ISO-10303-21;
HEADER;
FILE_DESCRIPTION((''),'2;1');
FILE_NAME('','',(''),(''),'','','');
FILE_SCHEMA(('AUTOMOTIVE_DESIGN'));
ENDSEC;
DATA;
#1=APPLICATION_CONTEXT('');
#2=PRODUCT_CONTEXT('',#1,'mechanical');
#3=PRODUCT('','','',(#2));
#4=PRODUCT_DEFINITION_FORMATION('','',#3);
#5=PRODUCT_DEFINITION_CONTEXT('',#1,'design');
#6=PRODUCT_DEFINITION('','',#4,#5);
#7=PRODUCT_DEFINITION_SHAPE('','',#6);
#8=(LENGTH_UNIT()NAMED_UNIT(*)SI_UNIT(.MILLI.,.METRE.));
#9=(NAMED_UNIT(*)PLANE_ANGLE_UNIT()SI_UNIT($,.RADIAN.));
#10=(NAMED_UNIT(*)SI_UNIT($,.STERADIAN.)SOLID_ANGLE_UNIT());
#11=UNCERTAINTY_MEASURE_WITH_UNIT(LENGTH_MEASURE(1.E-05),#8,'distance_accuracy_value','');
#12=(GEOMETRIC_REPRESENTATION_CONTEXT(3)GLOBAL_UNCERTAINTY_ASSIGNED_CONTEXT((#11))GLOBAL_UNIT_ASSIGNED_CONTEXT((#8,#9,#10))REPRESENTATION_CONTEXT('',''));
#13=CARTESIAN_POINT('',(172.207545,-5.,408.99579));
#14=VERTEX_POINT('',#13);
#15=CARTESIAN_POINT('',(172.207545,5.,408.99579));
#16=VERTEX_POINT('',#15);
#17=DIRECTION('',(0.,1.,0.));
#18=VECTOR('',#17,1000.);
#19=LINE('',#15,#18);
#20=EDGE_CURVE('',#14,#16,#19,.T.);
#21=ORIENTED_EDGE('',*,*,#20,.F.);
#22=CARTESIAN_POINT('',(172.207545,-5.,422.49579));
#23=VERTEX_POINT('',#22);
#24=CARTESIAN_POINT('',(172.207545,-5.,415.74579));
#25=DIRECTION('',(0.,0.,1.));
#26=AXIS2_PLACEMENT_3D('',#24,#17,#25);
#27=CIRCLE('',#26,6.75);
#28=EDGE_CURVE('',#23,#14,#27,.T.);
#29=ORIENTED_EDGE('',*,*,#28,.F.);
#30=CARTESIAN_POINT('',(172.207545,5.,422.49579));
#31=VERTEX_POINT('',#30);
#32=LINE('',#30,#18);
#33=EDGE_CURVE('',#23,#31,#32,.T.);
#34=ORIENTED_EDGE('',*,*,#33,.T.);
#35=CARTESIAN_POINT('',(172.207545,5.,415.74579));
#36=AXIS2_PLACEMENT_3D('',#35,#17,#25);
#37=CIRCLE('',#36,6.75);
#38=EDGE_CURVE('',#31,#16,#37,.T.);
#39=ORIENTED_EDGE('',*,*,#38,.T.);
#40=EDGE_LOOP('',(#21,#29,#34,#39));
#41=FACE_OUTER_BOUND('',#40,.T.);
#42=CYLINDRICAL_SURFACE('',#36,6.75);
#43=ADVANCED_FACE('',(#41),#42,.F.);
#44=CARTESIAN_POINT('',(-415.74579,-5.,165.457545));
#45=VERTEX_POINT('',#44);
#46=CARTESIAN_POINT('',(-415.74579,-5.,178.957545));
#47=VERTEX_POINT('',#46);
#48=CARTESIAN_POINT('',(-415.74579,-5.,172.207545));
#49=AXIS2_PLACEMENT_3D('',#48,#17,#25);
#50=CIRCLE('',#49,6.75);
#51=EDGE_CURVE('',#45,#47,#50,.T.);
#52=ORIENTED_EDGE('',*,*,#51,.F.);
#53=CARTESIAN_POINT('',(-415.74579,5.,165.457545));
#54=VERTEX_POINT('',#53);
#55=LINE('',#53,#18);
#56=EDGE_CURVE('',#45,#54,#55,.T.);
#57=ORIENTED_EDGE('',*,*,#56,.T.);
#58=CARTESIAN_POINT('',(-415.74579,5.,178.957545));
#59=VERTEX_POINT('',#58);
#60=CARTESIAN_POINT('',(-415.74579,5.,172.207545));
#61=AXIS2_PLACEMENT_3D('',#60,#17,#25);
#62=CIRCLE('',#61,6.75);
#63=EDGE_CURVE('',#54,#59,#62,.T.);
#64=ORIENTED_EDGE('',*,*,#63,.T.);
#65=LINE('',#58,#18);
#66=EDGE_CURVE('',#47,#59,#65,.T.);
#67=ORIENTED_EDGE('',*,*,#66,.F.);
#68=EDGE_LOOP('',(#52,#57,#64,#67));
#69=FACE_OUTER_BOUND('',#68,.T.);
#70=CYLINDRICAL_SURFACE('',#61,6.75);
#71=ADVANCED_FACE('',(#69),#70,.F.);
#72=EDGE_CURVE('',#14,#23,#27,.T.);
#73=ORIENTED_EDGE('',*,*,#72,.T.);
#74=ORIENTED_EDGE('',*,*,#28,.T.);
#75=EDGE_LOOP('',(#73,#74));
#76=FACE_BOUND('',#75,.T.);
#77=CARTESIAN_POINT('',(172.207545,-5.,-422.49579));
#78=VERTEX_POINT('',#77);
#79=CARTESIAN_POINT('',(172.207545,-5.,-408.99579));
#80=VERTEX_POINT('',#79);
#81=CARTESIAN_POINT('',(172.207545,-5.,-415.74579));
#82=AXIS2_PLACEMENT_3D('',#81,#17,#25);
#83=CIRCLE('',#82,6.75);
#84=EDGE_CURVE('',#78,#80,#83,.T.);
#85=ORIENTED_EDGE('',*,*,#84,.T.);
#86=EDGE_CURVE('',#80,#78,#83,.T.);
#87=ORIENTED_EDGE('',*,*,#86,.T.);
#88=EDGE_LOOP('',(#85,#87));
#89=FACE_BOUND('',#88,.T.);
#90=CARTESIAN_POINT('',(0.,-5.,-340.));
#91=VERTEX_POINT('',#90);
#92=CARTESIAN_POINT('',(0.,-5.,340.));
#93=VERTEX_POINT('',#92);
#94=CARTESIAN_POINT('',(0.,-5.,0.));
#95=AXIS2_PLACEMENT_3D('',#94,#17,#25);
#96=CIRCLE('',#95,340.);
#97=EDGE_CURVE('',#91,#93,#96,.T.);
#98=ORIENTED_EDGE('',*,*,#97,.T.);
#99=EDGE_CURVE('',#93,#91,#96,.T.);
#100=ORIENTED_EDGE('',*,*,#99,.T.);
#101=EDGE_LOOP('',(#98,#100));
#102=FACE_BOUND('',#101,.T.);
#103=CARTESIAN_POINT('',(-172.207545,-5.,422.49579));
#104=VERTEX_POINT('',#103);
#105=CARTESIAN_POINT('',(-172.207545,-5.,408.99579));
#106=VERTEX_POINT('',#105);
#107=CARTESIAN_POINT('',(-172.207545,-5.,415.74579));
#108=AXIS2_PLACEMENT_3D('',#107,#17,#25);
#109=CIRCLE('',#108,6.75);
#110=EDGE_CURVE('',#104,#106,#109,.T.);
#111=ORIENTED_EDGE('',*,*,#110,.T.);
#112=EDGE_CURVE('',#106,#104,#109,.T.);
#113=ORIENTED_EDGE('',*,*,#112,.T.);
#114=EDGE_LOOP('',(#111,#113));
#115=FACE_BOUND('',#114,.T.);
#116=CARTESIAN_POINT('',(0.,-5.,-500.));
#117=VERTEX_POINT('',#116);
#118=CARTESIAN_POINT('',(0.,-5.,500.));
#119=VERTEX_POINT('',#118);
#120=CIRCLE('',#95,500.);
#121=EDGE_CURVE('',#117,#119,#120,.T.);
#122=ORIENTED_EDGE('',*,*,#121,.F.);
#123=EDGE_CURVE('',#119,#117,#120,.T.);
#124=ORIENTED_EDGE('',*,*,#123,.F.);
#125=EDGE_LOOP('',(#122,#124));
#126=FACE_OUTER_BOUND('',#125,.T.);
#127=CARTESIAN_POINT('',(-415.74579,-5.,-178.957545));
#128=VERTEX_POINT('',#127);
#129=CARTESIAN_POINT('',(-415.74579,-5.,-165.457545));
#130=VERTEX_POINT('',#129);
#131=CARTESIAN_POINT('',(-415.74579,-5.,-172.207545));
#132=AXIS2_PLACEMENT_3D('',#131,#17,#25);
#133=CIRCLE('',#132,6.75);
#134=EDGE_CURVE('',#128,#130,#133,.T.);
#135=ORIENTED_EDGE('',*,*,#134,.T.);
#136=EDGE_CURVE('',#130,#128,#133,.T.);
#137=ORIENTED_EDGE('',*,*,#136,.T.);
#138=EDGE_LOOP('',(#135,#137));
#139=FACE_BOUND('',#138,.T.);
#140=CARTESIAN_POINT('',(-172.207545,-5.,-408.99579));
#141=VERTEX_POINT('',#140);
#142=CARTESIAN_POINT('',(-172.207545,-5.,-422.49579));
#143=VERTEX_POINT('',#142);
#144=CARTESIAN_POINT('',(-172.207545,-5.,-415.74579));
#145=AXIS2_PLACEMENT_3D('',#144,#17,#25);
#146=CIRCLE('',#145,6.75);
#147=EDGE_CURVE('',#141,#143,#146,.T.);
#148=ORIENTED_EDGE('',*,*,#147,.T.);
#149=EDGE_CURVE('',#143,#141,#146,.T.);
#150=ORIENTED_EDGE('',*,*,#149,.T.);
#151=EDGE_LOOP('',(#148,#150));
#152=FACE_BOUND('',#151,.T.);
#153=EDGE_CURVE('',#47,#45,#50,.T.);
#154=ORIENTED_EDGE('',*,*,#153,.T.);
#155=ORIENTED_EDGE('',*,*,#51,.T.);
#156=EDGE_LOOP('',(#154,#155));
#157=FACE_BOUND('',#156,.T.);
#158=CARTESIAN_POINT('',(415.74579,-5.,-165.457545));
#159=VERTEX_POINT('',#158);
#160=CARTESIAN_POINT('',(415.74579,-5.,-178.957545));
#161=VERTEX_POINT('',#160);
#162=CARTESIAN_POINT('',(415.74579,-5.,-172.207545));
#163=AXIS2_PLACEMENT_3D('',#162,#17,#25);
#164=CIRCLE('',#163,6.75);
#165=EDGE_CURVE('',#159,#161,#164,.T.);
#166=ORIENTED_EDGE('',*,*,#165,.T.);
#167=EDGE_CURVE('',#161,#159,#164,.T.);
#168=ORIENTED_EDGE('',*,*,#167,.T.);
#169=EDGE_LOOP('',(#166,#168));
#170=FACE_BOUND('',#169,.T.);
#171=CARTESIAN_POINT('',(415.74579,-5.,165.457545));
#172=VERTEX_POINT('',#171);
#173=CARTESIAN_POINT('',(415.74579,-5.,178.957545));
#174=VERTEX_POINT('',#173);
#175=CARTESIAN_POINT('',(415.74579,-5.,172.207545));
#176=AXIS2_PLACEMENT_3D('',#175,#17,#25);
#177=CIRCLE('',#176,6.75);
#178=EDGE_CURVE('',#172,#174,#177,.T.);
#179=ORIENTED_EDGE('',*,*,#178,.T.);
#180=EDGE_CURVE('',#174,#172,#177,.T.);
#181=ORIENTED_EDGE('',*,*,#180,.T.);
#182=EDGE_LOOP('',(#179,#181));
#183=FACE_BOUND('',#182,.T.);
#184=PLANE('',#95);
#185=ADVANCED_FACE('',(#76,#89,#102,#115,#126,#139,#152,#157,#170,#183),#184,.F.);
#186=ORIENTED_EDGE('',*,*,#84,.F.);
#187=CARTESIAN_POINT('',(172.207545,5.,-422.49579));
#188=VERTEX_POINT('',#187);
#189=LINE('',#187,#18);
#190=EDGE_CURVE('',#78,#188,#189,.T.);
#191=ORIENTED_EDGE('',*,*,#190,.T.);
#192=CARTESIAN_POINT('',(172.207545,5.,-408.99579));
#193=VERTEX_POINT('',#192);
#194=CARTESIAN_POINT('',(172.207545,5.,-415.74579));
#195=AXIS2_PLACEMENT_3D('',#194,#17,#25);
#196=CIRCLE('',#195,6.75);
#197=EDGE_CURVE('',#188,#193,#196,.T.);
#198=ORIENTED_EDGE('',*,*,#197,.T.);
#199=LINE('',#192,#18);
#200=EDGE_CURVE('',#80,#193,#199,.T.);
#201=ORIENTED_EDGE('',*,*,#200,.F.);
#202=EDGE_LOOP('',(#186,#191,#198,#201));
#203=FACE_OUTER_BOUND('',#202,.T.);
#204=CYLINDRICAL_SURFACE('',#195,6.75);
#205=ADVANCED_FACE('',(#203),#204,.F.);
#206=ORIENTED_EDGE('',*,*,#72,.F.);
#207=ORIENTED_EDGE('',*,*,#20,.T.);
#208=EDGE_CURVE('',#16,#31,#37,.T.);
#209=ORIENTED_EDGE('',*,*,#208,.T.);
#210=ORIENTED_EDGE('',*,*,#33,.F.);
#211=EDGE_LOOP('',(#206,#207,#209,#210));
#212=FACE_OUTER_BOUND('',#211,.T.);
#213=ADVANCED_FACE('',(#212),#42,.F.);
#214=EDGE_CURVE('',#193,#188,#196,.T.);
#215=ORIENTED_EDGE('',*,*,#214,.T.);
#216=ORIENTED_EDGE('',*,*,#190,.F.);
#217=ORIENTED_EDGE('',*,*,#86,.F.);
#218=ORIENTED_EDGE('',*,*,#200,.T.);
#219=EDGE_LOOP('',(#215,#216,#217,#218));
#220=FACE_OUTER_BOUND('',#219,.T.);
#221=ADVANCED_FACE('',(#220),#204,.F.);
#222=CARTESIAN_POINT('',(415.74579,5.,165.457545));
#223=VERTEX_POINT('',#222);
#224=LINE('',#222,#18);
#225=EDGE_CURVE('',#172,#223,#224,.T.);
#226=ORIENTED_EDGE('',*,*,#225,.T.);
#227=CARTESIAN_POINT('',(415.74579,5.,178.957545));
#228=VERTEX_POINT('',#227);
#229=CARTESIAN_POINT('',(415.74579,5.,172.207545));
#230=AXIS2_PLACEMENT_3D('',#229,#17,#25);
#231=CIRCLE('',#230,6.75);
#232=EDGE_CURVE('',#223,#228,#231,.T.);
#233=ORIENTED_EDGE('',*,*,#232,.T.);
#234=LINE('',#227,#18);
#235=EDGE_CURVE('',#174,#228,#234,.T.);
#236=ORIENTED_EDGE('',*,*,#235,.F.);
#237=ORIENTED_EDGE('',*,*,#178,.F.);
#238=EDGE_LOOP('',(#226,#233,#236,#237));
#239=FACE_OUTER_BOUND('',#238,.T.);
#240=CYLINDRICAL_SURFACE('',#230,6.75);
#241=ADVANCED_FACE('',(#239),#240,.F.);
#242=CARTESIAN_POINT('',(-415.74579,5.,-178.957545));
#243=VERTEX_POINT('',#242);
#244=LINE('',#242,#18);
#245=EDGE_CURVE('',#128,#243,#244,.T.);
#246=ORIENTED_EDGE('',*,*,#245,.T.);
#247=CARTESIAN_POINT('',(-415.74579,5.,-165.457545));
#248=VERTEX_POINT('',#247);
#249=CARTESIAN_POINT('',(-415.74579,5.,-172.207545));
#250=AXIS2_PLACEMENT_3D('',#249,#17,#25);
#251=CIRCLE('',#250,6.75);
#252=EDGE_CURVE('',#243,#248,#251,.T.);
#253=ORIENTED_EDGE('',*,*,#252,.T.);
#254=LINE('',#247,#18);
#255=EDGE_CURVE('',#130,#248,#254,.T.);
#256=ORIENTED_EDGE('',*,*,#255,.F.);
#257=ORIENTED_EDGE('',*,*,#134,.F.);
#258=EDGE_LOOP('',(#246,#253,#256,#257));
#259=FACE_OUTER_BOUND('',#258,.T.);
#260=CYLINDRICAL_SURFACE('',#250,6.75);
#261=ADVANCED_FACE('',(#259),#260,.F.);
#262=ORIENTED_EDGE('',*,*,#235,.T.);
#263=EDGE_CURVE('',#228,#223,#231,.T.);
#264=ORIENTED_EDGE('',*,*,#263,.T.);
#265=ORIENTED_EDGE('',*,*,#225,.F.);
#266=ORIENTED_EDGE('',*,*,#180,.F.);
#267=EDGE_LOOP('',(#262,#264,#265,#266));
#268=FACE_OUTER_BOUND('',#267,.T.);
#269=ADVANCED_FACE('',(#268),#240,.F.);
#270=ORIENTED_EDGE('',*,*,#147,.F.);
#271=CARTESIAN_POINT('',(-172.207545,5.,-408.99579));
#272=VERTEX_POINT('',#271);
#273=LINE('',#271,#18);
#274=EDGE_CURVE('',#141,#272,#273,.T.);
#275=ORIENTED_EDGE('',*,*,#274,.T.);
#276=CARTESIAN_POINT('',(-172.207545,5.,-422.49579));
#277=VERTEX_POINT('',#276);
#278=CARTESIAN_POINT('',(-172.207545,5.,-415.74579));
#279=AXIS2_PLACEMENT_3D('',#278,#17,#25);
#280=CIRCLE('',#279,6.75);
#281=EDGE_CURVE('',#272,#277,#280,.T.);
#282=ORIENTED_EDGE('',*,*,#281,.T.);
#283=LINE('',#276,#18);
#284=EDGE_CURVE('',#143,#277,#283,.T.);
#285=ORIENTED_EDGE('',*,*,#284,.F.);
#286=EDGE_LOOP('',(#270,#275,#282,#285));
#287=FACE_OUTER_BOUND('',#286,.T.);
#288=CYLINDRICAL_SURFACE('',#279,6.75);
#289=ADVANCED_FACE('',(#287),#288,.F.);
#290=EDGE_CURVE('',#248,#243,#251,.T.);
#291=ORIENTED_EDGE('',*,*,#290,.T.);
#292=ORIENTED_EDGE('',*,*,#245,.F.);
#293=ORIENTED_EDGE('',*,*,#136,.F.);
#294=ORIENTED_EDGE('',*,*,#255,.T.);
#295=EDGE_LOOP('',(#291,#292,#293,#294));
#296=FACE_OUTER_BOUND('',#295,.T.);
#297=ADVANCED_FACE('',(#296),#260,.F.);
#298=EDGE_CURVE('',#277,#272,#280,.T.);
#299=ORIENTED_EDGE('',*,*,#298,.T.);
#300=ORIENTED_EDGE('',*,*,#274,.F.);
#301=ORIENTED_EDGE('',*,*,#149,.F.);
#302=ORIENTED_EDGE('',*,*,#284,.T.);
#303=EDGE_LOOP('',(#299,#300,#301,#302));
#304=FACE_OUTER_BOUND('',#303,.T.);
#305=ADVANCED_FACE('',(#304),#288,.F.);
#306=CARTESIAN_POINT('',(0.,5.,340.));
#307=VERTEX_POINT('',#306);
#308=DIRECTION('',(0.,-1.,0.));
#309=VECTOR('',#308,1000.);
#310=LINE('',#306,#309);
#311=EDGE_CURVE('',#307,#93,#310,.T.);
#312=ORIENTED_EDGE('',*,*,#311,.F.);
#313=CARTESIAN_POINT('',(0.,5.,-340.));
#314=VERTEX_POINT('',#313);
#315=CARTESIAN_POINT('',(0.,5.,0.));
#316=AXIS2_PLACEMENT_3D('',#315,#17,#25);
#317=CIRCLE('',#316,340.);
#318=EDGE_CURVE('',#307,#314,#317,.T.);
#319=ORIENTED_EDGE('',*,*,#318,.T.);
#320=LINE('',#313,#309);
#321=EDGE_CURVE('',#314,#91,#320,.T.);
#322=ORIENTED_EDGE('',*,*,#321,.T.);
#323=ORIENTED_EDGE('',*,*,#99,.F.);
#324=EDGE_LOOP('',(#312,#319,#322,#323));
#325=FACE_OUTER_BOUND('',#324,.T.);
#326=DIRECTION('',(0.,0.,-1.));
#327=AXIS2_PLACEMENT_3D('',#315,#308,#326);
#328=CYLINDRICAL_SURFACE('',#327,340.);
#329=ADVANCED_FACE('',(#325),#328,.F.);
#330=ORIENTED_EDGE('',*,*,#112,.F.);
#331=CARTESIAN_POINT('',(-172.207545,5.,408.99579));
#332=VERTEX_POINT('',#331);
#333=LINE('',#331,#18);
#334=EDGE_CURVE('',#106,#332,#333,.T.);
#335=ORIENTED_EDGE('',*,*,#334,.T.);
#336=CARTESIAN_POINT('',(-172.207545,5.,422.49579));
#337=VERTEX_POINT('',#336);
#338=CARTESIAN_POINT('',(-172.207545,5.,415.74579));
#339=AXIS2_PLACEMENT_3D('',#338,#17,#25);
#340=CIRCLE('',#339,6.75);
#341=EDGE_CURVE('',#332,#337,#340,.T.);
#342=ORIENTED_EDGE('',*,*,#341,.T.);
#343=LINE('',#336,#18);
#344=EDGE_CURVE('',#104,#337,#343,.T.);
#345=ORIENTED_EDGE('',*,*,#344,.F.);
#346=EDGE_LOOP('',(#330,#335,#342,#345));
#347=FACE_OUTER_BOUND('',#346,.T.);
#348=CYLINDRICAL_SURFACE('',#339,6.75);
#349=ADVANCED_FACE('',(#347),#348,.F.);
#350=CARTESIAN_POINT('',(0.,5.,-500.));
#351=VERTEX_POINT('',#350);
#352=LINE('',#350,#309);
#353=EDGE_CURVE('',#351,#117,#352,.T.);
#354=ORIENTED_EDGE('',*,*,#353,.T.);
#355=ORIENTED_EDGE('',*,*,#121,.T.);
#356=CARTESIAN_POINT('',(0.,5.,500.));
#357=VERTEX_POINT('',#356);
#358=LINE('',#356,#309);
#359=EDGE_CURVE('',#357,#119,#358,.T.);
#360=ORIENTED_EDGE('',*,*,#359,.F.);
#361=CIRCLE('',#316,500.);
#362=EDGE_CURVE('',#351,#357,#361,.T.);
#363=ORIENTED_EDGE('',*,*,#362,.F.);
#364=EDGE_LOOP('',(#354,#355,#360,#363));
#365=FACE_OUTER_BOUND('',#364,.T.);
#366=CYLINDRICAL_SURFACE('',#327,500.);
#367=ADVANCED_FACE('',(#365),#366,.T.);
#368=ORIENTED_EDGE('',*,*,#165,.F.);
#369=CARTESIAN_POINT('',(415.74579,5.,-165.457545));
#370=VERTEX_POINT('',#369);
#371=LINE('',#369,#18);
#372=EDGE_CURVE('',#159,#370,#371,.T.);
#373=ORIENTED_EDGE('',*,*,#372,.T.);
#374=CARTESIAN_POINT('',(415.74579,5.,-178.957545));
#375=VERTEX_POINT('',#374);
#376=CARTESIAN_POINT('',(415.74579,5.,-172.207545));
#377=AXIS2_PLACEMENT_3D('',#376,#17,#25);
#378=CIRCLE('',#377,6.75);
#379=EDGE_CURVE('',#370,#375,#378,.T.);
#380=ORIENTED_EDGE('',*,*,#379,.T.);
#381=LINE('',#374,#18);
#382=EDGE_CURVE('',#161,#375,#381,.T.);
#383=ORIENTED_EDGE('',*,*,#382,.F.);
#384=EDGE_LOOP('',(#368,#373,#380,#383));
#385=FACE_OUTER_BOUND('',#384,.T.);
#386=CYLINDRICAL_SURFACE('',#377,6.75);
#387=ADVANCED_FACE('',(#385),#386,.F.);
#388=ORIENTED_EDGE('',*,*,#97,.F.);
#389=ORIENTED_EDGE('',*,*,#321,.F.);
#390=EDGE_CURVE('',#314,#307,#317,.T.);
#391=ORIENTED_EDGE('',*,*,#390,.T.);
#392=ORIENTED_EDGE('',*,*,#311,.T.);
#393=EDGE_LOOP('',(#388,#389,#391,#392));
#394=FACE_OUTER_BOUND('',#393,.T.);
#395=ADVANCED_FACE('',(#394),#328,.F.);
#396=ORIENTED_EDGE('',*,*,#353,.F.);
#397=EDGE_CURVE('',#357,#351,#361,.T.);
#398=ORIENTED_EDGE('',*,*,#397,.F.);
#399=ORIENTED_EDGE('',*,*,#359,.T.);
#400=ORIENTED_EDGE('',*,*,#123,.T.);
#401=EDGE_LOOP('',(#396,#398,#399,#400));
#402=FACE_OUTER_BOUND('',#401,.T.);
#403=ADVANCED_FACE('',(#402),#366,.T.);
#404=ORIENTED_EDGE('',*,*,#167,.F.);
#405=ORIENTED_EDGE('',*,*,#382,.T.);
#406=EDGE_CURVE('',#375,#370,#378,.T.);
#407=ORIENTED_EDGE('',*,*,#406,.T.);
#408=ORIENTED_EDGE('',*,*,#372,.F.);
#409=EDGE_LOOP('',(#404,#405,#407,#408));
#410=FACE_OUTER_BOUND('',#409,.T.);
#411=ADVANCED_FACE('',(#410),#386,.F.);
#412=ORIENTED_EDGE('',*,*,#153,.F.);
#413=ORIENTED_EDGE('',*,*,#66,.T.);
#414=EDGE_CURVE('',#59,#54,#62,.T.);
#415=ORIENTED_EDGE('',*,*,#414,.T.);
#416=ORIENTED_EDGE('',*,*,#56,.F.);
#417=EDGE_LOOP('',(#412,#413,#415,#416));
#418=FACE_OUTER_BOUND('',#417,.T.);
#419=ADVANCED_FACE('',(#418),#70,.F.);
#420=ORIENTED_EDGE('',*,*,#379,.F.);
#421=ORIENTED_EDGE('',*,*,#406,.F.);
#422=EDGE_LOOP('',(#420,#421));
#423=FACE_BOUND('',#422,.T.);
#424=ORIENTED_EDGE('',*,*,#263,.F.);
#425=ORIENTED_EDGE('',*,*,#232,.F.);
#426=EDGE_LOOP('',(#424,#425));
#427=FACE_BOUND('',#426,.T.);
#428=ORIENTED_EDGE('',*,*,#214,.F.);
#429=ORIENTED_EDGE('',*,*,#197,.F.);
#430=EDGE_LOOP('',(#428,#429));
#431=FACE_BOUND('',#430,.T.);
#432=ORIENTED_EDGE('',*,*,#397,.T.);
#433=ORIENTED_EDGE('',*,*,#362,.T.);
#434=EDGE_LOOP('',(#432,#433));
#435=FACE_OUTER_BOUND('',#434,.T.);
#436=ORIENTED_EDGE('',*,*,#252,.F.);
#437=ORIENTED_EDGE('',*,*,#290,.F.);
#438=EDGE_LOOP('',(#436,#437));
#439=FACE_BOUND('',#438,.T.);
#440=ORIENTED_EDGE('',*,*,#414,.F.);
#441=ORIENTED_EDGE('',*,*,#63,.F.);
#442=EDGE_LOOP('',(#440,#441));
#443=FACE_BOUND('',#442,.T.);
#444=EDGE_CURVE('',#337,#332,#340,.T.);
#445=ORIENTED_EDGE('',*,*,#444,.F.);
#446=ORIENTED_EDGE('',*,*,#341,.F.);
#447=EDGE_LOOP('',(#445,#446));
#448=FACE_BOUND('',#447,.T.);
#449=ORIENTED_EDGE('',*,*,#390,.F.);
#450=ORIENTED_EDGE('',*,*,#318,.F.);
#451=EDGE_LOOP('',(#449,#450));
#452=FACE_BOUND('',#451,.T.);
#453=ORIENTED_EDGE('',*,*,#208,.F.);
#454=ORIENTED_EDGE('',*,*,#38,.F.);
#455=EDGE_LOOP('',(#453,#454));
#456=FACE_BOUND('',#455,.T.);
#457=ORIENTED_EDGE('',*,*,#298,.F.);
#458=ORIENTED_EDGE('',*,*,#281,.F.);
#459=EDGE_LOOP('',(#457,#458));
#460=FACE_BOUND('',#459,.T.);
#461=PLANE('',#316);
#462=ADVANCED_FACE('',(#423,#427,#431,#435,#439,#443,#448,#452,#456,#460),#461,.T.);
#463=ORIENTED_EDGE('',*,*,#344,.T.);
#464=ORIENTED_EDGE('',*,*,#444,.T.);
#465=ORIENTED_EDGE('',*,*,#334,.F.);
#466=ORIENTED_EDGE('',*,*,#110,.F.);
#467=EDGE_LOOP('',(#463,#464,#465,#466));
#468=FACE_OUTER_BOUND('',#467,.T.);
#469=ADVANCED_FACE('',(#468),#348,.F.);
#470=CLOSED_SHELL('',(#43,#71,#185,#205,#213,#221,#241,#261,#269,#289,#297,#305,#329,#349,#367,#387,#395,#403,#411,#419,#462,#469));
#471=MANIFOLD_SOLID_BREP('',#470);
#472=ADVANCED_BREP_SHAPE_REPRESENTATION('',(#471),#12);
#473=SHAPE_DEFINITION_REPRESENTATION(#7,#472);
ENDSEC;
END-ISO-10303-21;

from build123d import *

# Parameters (mm, degrees)
SKETCH1_R                    = 500
SKETCH1_R_2                  = 340
BOSS_EXTRUDE1_DEPTH          = 5
F_13_5_13_5_DIAMETER_HOLE1_D = 13.5


with BuildPart() as part:
    # Sketch1 → Boss-Extrude1 (new, symmetric)
    with BuildSketch(Plane(origin=(0, 0, 0), x_dir=(1, 0, 0), z_dir=(0, 1, 0))):
        with Locations(Location((0, 0, 0), (0, 0, 270))):
            Circle(SKETCH1_R)
        with Locations(Location((0, 0, 0), (0, 0, 270))):
            Circle(SKETCH1_R_2, mode=Mode.SUBTRACT)
    extrude(amount=BOSS_EXTRUDE1_DEPTH, both=True)

    # Ø13.5 (13.5) Diameter Hole1 (through all)
    with Locations(Plane(origin=(0, 5, 0), x_dir=(1, 0, 0), z_dir=(0, 1, 0))):
        with Locations((172.207544564, 415.74578963), (415.74578963, 172.207544564), (415.74578963, -172.207544564), (172.207544564, -415.74578963), (-172.207544564, -415.74578963), (-415.74578963, -172.207544564), (-415.74578963, 172.207544564), (-172.207544564, 415.74578963)):
            Hole(F_13_5_13_5_DIAMETER_HOLE1_D / 2)


solid = part.part
